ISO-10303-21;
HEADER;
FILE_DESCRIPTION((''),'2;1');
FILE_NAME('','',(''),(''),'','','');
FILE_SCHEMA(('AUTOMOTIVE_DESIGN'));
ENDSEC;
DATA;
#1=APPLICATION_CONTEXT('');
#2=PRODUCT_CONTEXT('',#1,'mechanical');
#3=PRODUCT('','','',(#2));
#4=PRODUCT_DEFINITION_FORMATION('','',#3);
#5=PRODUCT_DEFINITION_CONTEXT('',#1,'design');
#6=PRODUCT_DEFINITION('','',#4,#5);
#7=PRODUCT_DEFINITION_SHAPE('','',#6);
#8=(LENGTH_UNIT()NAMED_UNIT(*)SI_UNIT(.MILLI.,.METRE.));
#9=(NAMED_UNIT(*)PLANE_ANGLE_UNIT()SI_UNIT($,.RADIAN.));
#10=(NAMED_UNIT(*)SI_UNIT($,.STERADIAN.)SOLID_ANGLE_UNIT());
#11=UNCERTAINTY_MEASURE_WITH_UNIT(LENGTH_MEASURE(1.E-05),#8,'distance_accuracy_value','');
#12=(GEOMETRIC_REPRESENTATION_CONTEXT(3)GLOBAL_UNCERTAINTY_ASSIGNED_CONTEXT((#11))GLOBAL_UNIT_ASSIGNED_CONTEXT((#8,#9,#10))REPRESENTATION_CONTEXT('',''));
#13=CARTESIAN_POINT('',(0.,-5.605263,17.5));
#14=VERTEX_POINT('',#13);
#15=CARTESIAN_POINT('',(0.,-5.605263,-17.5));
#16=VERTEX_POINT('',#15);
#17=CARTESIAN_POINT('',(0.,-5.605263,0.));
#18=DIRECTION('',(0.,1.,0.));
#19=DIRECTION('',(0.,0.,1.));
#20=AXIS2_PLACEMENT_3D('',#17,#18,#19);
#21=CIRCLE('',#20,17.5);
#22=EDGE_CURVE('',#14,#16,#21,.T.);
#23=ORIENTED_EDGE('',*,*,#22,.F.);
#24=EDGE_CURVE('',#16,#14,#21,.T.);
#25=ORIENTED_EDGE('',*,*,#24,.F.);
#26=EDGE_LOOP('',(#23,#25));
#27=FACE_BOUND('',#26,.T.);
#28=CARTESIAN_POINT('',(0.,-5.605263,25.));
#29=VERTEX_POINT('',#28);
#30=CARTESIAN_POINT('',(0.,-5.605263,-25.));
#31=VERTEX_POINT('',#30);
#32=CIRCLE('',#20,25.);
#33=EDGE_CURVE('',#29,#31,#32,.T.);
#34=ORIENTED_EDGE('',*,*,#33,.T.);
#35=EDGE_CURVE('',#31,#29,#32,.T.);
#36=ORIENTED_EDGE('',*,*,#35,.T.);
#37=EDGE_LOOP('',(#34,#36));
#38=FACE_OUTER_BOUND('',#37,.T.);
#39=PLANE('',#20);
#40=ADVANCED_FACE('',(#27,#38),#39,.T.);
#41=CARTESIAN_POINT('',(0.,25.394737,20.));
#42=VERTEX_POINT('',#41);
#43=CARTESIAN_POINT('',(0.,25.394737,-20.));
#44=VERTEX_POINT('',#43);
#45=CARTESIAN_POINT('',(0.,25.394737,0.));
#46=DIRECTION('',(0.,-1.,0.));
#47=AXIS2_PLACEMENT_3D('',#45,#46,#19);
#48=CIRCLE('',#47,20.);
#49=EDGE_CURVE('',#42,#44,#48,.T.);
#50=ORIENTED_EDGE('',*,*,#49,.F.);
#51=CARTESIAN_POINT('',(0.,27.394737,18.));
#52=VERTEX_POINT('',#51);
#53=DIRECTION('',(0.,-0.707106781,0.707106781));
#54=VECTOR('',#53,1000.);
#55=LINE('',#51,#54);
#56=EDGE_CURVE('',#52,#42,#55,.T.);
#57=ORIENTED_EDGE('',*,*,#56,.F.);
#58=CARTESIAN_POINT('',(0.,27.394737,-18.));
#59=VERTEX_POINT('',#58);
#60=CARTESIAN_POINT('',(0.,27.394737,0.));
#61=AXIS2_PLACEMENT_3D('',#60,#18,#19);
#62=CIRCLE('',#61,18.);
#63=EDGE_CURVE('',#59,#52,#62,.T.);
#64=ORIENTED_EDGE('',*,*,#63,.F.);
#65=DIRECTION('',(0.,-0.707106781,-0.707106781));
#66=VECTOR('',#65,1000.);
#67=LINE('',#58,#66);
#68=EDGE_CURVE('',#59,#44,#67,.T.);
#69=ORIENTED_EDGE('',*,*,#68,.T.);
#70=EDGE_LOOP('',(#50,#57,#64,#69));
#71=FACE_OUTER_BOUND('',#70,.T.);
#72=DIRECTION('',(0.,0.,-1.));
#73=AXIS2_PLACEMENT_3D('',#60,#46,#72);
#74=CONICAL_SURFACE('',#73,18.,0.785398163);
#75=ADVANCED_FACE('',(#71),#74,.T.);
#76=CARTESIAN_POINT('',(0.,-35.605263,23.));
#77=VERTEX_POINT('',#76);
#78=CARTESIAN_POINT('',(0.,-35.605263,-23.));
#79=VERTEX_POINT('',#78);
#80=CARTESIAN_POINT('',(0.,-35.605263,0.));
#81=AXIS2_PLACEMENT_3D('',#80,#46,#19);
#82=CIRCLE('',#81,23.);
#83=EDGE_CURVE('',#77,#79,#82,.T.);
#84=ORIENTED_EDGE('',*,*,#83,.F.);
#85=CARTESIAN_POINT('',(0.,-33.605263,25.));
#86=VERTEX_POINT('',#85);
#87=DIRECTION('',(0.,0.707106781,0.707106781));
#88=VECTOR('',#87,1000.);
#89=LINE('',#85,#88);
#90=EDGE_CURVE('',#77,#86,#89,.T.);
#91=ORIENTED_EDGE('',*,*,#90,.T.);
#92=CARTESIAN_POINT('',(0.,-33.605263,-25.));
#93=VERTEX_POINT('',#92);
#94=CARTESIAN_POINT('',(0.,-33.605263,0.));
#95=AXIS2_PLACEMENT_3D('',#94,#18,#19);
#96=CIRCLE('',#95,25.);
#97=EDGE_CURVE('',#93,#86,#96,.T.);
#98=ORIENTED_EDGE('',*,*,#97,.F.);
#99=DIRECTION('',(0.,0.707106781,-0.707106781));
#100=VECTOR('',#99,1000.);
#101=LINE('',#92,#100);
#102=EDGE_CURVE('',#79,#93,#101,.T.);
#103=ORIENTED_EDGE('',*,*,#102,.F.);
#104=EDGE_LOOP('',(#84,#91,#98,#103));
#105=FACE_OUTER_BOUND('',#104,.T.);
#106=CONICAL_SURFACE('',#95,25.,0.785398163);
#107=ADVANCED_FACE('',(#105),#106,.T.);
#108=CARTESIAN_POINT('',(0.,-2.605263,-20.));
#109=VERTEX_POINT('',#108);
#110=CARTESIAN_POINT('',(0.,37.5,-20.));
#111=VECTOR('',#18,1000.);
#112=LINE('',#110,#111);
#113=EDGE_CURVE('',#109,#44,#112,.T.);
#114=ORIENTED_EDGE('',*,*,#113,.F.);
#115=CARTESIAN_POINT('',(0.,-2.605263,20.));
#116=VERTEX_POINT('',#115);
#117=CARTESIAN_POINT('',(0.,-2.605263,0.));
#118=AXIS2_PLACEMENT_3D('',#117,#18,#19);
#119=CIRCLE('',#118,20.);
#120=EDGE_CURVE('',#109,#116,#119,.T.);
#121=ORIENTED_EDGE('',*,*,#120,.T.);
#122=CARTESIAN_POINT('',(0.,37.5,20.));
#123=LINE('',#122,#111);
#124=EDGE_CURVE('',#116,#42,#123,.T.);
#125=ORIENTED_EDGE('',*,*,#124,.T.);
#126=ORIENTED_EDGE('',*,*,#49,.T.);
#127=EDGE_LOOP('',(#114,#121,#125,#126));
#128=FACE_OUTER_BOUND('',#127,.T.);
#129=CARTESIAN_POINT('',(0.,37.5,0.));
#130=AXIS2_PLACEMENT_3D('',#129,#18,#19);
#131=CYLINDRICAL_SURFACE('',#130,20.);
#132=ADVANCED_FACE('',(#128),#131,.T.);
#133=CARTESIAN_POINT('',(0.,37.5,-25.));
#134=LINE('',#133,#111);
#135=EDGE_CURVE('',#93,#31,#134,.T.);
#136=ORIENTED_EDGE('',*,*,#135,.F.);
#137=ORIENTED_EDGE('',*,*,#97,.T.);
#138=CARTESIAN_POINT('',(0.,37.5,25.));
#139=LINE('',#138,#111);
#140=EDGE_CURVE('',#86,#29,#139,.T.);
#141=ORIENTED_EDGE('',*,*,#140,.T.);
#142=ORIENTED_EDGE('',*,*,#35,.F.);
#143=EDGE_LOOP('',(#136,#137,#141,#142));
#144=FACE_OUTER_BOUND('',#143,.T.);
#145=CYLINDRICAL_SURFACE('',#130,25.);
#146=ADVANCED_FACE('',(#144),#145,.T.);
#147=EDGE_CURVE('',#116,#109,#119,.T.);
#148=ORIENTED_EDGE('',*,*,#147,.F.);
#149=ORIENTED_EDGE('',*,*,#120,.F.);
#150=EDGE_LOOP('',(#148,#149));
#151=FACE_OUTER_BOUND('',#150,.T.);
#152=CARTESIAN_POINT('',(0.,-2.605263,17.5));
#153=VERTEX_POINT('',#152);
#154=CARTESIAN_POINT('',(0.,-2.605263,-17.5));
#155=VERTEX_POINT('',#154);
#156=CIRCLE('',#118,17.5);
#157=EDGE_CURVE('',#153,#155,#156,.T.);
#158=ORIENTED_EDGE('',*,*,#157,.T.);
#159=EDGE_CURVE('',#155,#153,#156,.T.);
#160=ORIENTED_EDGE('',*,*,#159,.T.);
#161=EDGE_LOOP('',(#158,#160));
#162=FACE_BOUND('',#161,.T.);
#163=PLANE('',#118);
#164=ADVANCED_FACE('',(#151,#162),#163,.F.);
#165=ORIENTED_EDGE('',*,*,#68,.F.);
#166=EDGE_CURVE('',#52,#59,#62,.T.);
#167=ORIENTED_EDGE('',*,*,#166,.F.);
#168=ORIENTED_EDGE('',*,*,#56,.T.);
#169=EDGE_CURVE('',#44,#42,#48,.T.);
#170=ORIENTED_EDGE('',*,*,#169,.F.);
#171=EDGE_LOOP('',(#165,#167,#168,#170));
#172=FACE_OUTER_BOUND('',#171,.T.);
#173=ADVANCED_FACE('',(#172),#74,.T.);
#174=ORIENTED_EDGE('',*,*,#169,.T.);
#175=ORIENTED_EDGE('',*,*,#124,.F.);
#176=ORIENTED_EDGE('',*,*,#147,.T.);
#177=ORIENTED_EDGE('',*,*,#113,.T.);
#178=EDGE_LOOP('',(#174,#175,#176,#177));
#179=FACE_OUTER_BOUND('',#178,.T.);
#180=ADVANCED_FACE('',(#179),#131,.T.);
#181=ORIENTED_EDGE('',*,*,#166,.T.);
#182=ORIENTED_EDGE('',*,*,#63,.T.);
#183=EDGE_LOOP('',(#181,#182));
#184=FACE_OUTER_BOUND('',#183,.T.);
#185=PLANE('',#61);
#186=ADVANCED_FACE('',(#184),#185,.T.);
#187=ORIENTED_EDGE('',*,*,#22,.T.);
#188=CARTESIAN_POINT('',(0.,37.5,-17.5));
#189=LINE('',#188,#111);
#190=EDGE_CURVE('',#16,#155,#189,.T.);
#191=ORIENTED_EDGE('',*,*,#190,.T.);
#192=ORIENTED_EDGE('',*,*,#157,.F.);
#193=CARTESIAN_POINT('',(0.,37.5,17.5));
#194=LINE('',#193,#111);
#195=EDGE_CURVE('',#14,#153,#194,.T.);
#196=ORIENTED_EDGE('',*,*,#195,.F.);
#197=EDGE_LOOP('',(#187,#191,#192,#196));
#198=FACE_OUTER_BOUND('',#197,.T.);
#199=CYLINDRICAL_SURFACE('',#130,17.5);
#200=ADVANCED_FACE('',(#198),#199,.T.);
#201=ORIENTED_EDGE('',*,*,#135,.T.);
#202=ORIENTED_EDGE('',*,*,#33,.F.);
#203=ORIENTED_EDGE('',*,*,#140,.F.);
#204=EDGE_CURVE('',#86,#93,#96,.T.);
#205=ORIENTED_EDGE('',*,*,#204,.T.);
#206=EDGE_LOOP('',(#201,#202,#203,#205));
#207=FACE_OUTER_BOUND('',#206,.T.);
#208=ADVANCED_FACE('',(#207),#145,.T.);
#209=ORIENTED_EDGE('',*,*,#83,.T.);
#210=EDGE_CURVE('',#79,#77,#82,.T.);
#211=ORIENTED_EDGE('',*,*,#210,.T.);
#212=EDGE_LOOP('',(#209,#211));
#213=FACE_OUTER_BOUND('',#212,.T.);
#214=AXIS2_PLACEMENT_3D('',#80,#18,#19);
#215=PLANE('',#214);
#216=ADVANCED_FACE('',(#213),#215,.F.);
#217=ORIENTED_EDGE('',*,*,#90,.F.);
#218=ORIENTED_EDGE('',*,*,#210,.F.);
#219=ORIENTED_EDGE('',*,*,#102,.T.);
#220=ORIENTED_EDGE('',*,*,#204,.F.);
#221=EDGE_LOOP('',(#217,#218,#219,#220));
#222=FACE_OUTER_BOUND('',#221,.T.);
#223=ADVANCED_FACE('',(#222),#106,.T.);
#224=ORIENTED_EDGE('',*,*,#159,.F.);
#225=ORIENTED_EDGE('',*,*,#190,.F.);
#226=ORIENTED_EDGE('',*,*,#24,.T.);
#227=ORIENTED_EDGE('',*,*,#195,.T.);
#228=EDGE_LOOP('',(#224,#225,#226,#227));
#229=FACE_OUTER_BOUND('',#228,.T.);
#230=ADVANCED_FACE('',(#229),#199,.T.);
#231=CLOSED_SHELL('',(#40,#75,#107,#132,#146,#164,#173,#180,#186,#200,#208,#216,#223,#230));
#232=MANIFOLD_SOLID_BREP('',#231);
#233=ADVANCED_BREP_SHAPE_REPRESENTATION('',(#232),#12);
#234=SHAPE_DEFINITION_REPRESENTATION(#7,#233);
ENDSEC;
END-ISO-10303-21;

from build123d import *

# Parameters (mm, degrees)
SKETCH1_W     = 20
SKETCH1_H     = 30
SKETCH1_W_2   = 17.5
SKETCH1_H_2   = 3
CHAMFER1_SIZE = 2
CHAMFER2_SIZE = 2


with BuildPart() as part:
    # Sketch1 → Revolve1 (revolve)
    with BuildSketch(Plane.XY, mode=Mode.PRIVATE) as revolve1_sk:
        Polygon((0, -35.605263158), (0, -5.605263158), (-17.5, -5.605263158), (-25, -5.605263158), (-25, -35.605263158), align=None)
        with Locations((-10, 12.394736842)):
            Rectangle(SKETCH1_W, SKETCH1_H)
        with Locations((-8.75, -4.105263158)):
            Rectangle(SKETCH1_W_2, SKETCH1_H_2)
    revolve(revolve1_sk.sketch.rotate(Axis((0, 37.5, 0), (0, -1, 0)), 270), axis=Axis((0, 37.5, 0), (0, -1, 0)))

    # Chamfer1
    chamfer1_edges = [part.edges().sort_by_distance(p)[0] for p in [
        (0, 27.394736842, -20),
    ]]
    chamfer(chamfer1_edges, length=CHAMFER1_SIZE)

    # Chamfer2
    chamfer2_edges = [part.edges().sort_by_distance(p)[0] for p in [
        (0, -35.605263158, -25),
    ]]
    chamfer(chamfer2_edges, length=CHAMFER2_SIZE)


solid = part.part
